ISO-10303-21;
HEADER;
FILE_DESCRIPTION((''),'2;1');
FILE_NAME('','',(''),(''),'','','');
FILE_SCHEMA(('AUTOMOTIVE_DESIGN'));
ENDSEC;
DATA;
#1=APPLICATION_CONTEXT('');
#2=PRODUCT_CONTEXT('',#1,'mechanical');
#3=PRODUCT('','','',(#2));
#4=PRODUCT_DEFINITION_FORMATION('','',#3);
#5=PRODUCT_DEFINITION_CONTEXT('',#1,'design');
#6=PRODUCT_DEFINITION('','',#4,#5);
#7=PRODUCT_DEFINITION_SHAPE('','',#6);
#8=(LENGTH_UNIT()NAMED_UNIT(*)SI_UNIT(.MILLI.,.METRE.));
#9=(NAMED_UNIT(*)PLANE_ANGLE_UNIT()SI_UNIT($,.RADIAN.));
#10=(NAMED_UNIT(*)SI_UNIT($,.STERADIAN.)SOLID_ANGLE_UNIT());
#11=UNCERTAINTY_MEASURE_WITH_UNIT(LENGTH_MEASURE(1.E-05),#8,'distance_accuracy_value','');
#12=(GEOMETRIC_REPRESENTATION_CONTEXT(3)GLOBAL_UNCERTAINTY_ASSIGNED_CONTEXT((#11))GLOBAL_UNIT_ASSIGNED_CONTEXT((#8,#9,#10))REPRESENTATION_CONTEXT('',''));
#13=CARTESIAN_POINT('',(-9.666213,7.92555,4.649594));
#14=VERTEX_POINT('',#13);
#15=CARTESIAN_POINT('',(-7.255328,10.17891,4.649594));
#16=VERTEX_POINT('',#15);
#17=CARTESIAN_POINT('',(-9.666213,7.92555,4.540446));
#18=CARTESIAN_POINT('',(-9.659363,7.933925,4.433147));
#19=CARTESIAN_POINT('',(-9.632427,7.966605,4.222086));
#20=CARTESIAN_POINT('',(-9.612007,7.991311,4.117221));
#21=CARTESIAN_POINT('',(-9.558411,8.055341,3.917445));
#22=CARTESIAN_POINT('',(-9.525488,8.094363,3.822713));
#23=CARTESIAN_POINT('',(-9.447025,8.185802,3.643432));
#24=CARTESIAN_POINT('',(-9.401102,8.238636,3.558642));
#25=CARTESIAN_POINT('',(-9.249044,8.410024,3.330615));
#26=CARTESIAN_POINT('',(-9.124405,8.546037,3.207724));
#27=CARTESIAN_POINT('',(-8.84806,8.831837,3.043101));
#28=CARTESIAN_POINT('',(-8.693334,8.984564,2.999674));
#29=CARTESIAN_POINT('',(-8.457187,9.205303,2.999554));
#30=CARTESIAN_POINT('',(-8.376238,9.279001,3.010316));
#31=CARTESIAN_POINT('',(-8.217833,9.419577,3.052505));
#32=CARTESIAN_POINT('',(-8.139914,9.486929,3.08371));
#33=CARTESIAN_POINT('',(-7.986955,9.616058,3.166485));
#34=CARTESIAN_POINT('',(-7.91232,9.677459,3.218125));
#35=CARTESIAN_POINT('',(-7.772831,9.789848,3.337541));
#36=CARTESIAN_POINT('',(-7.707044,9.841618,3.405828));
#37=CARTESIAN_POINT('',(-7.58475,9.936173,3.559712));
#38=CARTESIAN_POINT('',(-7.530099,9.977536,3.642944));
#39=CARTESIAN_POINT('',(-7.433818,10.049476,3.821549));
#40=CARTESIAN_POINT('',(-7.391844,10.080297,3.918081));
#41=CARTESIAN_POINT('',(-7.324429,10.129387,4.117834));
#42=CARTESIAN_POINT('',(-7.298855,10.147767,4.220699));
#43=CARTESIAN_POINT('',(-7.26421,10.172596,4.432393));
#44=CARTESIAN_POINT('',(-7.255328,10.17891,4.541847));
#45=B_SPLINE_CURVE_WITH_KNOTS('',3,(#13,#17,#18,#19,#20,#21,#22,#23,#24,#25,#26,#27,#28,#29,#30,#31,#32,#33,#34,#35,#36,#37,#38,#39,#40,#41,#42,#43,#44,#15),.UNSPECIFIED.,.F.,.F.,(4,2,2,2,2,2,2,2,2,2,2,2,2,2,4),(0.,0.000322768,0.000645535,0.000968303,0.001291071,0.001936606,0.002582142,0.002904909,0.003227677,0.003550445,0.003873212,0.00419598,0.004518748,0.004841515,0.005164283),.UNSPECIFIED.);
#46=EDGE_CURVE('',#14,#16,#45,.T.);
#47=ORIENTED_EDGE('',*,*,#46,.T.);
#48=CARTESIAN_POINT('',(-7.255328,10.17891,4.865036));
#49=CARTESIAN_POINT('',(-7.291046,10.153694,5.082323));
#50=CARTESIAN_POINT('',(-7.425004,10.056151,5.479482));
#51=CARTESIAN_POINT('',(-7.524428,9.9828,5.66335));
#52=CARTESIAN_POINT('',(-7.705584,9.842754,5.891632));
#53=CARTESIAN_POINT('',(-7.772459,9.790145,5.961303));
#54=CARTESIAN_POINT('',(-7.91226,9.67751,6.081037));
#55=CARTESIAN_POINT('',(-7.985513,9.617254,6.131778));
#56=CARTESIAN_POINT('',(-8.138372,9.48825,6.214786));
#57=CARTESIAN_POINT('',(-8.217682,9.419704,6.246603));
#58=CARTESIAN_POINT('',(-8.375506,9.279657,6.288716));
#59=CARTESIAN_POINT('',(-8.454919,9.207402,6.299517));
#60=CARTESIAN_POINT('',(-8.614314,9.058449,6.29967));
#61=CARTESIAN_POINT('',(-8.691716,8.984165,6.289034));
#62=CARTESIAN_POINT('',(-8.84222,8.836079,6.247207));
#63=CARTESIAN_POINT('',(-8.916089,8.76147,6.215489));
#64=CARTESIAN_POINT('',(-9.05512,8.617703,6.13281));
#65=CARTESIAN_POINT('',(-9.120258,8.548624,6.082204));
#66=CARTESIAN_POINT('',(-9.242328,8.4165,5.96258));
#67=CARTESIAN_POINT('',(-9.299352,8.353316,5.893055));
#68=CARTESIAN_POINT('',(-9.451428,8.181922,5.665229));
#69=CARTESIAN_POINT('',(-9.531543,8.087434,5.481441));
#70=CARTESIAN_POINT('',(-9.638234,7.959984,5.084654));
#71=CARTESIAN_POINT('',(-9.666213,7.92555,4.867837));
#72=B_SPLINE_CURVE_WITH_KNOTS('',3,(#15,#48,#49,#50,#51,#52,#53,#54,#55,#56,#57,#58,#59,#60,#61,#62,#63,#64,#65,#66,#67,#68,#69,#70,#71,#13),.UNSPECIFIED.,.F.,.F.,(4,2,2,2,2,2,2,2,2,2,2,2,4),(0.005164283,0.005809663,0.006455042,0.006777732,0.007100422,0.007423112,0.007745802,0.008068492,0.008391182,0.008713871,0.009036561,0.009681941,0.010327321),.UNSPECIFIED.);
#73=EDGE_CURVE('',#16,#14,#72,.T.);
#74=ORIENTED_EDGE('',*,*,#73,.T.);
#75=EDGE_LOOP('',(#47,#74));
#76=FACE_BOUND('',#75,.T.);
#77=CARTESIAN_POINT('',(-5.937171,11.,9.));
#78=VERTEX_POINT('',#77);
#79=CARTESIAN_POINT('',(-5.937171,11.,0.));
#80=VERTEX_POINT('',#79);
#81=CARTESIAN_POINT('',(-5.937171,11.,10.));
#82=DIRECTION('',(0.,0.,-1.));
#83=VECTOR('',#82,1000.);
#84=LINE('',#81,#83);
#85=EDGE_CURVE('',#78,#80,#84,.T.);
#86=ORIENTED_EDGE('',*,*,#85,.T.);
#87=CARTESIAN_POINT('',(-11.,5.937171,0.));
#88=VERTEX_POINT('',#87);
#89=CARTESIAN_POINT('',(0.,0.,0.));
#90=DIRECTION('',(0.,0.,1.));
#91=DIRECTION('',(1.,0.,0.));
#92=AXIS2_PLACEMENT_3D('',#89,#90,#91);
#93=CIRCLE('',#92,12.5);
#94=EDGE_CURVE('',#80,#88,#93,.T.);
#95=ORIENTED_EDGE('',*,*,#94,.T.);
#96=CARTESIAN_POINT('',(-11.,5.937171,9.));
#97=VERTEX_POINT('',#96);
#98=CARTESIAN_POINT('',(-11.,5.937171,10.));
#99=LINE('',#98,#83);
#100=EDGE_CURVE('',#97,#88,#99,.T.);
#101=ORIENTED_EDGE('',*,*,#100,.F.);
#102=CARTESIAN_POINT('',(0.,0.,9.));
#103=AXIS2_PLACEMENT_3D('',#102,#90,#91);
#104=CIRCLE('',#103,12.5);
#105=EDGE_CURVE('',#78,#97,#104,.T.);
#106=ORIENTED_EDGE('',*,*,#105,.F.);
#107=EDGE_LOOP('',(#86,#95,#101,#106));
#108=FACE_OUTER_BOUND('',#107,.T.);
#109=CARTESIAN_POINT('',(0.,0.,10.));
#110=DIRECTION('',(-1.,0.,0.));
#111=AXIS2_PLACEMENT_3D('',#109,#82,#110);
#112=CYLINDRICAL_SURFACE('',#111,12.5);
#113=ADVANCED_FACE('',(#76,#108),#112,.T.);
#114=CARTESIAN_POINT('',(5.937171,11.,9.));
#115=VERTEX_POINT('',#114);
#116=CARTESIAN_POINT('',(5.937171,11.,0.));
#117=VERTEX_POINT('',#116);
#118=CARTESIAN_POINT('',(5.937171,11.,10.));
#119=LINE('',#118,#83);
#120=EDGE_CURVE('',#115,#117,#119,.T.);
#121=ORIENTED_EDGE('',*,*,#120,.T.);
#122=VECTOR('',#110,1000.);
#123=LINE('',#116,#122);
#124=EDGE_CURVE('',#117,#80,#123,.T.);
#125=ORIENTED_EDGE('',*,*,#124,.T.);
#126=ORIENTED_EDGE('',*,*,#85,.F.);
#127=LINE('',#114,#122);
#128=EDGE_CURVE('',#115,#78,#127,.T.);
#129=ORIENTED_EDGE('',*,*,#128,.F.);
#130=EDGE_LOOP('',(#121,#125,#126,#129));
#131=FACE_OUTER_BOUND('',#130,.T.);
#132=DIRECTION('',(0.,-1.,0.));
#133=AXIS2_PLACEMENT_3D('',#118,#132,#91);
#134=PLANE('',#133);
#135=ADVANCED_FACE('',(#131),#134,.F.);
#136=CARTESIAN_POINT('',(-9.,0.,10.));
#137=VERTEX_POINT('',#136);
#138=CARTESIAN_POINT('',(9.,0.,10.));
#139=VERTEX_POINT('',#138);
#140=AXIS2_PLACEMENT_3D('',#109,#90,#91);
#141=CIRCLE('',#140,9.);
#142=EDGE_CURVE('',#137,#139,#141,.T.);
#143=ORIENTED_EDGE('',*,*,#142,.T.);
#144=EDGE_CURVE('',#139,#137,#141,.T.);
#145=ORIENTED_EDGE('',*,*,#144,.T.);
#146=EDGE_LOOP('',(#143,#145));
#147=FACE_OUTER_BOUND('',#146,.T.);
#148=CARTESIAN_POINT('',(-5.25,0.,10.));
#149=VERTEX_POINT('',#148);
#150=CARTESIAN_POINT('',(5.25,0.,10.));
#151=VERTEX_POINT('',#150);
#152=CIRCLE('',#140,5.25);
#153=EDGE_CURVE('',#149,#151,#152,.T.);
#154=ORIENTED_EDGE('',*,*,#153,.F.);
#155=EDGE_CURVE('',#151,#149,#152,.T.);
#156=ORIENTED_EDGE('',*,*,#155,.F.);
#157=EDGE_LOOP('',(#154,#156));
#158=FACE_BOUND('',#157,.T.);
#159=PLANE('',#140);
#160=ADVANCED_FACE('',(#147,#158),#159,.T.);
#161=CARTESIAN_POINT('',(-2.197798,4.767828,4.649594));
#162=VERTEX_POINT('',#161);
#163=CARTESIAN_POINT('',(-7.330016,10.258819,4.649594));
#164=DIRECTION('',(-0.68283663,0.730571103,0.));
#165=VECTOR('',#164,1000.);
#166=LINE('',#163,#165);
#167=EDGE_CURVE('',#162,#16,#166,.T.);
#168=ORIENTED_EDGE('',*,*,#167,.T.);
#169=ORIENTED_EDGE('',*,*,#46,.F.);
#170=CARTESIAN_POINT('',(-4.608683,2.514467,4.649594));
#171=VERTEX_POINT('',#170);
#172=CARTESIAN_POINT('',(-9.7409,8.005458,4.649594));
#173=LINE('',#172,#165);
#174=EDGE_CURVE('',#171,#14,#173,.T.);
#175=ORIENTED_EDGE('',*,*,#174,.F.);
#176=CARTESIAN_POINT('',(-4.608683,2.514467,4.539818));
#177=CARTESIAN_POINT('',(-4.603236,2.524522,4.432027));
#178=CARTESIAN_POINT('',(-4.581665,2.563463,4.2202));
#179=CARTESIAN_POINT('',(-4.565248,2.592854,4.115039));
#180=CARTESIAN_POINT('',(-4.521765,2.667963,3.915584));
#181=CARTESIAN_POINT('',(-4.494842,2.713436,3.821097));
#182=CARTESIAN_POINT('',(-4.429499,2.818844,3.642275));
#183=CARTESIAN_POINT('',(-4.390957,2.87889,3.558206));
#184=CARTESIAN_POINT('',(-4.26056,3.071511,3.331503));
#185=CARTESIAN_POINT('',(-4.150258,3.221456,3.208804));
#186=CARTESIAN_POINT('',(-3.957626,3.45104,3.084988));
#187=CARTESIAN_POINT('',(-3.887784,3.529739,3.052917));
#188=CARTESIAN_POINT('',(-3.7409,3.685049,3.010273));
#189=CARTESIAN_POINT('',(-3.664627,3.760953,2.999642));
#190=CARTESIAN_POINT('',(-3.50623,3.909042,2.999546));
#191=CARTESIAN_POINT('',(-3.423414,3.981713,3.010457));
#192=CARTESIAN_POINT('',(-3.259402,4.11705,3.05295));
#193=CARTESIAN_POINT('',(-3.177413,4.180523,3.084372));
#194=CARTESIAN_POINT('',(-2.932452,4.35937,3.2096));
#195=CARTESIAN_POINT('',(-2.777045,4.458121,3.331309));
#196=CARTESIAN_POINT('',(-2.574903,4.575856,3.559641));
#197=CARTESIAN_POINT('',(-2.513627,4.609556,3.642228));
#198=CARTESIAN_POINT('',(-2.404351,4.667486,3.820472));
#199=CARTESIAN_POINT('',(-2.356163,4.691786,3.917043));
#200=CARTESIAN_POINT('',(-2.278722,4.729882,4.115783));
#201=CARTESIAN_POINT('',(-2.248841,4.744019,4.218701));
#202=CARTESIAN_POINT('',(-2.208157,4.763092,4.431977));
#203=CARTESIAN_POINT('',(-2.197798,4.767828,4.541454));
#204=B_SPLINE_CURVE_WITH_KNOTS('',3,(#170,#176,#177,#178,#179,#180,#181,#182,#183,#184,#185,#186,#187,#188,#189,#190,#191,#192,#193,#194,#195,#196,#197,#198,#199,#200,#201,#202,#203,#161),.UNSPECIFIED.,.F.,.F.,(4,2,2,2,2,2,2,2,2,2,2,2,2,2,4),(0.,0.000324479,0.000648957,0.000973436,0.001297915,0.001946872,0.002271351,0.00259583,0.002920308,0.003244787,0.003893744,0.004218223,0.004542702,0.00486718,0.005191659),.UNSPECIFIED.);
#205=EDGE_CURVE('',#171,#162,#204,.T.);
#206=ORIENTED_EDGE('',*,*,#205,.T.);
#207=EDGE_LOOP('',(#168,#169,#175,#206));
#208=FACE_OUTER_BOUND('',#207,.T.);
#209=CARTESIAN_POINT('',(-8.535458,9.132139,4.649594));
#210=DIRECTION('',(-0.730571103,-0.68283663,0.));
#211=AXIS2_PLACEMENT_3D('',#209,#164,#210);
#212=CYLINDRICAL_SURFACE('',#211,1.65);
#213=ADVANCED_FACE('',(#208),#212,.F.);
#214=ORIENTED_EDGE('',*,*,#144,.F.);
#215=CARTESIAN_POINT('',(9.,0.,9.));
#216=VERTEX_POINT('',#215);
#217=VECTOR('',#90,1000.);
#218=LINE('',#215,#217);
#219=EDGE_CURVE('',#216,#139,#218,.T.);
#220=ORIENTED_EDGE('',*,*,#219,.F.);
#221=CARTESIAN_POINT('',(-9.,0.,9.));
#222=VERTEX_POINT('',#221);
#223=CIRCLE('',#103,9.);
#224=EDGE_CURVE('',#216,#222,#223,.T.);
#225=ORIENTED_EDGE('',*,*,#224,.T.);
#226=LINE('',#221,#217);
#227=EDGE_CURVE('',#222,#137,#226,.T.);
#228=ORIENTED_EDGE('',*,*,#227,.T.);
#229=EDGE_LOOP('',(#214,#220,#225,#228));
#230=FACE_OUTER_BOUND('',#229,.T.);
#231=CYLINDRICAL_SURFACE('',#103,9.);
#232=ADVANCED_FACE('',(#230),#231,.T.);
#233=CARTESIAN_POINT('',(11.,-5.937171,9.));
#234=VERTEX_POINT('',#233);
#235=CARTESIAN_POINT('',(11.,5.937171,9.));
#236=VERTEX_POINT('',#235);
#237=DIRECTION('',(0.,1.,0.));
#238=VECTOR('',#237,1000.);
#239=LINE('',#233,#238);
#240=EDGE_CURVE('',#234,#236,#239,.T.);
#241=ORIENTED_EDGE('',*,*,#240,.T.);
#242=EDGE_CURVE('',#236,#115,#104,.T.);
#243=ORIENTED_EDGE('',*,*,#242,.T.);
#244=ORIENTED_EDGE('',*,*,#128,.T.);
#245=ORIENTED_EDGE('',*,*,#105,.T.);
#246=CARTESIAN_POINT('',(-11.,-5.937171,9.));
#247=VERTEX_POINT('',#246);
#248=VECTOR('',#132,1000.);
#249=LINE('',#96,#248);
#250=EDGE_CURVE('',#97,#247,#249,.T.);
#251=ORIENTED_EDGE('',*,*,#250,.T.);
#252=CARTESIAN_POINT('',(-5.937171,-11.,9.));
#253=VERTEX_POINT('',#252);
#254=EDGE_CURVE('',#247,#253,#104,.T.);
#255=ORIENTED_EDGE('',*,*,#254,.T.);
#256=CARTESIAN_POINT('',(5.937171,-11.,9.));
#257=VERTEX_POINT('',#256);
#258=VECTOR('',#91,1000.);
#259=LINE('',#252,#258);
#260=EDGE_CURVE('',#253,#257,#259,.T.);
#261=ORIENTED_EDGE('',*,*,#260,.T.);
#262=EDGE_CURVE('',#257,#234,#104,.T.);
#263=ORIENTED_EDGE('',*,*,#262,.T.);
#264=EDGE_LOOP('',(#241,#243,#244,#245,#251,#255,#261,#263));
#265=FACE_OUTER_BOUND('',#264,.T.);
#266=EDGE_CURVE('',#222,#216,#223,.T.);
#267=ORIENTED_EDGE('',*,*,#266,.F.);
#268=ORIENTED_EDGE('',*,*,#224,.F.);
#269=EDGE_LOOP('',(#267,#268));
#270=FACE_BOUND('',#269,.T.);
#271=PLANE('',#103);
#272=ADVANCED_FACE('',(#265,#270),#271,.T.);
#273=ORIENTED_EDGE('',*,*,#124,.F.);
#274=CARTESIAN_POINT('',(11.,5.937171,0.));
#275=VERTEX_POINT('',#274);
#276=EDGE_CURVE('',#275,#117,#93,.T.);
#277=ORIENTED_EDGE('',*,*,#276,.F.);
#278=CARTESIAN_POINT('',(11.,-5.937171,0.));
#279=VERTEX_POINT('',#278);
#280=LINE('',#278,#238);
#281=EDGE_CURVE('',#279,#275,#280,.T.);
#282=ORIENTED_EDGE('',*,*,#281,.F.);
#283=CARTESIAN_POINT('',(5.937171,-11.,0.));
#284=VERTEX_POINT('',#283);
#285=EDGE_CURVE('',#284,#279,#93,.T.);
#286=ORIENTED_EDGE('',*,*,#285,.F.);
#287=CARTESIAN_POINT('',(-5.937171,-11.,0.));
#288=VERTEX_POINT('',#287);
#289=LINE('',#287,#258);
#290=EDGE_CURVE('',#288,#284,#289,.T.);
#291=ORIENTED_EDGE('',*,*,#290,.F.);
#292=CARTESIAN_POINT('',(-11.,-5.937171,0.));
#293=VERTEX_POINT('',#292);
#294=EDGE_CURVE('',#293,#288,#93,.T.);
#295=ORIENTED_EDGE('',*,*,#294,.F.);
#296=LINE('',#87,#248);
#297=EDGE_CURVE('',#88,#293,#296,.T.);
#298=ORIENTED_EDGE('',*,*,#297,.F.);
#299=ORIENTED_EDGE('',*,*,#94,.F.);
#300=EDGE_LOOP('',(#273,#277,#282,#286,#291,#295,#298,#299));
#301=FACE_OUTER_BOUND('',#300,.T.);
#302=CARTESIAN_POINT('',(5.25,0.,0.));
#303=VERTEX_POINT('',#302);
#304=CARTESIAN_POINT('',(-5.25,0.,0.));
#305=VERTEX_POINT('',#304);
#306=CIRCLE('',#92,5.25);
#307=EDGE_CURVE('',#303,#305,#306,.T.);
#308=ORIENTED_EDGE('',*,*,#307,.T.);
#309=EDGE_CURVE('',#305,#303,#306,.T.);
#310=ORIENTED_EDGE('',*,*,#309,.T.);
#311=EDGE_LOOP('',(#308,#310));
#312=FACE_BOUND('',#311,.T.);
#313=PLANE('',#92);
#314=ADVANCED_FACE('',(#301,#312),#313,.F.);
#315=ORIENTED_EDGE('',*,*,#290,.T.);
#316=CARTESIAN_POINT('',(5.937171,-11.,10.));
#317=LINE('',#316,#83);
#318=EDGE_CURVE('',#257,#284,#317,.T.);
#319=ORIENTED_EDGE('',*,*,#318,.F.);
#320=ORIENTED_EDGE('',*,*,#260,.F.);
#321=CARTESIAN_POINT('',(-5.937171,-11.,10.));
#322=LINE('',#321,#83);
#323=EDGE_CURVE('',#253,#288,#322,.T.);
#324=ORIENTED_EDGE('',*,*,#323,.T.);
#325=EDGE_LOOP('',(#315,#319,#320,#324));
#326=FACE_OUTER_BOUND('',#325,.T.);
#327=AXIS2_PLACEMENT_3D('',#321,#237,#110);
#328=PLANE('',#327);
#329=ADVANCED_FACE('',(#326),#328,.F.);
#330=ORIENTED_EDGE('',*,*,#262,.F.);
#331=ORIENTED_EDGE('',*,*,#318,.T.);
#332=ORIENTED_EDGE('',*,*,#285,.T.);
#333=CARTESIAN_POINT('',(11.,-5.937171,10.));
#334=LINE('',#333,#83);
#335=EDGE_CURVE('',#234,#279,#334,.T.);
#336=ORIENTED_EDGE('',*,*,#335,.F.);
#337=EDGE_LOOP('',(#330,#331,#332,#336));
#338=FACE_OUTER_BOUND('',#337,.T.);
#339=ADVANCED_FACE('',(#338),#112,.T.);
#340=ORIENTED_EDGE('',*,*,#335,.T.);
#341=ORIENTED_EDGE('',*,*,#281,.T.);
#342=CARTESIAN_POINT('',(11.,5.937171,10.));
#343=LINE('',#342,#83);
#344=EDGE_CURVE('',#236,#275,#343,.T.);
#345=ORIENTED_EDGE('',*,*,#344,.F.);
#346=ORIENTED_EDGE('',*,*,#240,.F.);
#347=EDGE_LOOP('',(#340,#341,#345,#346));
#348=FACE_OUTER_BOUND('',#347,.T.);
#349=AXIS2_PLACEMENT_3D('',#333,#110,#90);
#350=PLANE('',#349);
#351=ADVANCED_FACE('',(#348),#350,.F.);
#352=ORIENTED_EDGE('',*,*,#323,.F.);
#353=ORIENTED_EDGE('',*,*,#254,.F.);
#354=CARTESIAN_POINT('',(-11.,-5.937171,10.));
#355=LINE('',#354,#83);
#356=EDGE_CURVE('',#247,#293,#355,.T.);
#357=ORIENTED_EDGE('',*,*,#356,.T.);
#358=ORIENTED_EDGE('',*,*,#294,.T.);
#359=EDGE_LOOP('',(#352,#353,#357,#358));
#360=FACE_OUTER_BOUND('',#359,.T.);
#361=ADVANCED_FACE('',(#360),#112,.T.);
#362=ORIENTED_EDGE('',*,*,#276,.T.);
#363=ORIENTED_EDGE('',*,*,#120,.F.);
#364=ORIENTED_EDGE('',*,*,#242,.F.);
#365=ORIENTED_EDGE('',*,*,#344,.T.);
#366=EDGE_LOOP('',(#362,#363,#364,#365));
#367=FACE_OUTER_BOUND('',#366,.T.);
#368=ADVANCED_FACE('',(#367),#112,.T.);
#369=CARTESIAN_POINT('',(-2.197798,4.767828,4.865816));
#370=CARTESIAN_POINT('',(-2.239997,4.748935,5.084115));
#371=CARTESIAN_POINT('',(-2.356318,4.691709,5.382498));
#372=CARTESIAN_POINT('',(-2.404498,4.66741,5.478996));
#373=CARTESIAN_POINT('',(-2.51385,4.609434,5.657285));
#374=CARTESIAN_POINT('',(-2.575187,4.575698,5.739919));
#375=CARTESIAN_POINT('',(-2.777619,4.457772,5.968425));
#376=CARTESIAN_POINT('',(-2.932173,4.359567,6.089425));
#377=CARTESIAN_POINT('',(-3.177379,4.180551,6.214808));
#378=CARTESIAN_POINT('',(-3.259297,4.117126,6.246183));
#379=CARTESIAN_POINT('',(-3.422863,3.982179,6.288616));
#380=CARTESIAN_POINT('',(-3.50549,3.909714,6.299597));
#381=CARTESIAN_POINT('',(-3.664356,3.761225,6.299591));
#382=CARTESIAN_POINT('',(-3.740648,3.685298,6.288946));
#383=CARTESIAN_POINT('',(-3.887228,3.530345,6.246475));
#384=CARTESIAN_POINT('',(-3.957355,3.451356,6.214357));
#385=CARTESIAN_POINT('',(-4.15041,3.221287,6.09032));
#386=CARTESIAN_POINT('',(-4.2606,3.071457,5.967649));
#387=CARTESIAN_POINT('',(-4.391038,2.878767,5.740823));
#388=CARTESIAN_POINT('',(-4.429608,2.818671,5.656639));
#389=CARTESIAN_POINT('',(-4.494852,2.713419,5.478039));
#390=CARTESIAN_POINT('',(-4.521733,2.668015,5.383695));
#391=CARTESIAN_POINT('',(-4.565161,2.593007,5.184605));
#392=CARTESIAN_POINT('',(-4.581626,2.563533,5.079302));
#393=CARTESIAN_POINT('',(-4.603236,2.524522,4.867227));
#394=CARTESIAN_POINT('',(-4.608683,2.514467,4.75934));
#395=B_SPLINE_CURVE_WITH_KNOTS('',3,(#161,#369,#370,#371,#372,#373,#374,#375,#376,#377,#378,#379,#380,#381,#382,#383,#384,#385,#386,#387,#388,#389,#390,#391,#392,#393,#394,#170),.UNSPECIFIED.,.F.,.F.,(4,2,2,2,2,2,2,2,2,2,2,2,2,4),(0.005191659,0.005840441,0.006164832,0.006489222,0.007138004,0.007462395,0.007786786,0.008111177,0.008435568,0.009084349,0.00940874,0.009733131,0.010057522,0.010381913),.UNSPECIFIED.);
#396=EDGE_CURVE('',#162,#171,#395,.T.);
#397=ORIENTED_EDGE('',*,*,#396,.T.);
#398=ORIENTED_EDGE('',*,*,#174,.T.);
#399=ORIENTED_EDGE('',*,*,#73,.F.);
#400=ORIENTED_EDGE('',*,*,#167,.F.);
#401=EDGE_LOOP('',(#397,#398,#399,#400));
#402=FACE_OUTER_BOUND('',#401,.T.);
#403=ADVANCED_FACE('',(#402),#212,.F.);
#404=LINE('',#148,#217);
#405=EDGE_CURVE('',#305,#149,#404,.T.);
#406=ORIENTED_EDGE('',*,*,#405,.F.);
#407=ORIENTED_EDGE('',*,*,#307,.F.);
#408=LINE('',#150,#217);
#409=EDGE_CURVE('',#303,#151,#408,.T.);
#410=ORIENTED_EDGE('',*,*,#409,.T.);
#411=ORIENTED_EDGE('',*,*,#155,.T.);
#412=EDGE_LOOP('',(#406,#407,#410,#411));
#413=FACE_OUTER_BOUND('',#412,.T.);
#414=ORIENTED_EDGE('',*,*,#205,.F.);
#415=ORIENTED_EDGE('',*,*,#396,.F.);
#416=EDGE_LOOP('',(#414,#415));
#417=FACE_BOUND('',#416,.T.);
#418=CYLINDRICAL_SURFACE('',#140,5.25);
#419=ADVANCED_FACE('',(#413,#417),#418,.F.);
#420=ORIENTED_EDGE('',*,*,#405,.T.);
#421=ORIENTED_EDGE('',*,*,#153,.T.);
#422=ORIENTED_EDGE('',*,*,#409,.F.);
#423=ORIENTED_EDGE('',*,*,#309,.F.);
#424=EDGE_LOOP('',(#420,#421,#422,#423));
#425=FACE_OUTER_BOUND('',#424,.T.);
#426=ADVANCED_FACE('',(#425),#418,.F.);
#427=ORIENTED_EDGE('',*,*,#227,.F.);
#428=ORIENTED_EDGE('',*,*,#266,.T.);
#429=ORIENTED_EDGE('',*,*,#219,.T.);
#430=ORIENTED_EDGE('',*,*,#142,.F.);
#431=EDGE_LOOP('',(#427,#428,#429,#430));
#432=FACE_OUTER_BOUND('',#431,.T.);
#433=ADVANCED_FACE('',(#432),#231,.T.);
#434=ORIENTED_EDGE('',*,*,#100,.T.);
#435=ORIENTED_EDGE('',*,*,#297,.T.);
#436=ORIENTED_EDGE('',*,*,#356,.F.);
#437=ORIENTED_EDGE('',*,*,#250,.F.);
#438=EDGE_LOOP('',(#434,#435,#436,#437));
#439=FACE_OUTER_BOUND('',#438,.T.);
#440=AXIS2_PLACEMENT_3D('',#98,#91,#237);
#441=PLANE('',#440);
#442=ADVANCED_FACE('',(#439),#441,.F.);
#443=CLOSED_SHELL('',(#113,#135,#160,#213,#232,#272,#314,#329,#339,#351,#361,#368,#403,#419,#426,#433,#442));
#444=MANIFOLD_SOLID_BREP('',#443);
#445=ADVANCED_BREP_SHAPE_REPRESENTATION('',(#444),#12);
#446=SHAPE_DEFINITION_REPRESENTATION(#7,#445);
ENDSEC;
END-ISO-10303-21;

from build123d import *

# Parameters (mm, degrees)
EXTRUDE1_DEPTH             = 10
SKETCH2_OUTSIDE_W          = 30.536
SKETCH2_OUTSIDE_H          = 30.536
SKETCH2_OUTSIDE_R          = 9
EXTRUDE2_DEPTH             = 1
M4X0_7_TAPPED_HOLE1_D      = 3.3
M4X0_7_TAPPED_HOLE1_DEPTH  = 10.1
M4X0_7_TAPPED_HOLE1_TIP    = 0.991420021
M12X1_5_TAPPED_HOLE1_D     = 10.5
M12X1_5_TAPPED_HOLE1_DEPTH = 28.5
M12X1_5_TAPPED_HOLE1_TIP   = 3.15451825


with BuildPart() as part:
    # Sketch1 → Extrude1 (new body)
    with BuildSketch(Plane.XY):
        with BuildLine():
            Line((-5.937171043, -11), (5.937171043, -11))
            ThreePointArc((5.937171043, -11), (8.838834765, -8.838834765), (11, -5.937171043))
            Line((11, -5.937171043), (11, 5.937171043))
            ThreePointArc((11, 5.937171043), (8.838834765, 8.838834765), (5.937171043, 11))
            Line((5.937171043, 11), (-5.937171043, 11))
            ThreePointArc((-5.937171043, 11), (-8.838834765, 8.838834765), (-11, 5.937171043))
            Line((-11, 5.937171043), (-11, -5.937171043))
            ThreePointArc((-11, -5.937171043), (-8.838834765, -8.838834765), (-5.937171043, -11))
        make_face()
    extrude(amount=EXTRUDE1_DEPTH)

    # Sketch2 outside → Extrude2 (cut)
    with BuildSketch(Plane.XY.offset(10)):
        Rectangle(SKETCH2_OUTSIDE_W, SKETCH2_OUTSIDE_H)
        Circle(SKETCH2_OUTSIDE_R, mode=Mode.SUBTRACT)
    extrude(amount=-EXTRUDE2_DEPTH, mode=Mode.SUBTRACT)

    # M4x0.7 Tapped Hole1
    with Locations(Plane(origin=(-8.535457879, 9.132138785, 4.649594026), x_dir=(0.730571102805, 0.682836630349, 0), z_dir=(-0.682836630349, 0.730571102805, 0))):
        with Locations((0, 0)):
            Hole(M4X0_7_TAPPED_HOLE1_D / 2, depth=M4X0_7_TAPPED_HOLE1_DEPTH)
            with Locations((0, 0, -(M4X0_7_TAPPED_HOLE1_DEPTH + M4X0_7_TAPPED_HOLE1_TIP / 2))):  # 118° drill point
                Cone(0, M4X0_7_TAPPED_HOLE1_D / 2, M4X0_7_TAPPED_HOLE1_TIP, mode=Mode.SUBTRACT)

    # M12x1.5 Tapped Hole1
    with Locations(Plane.XY.offset(10)):
        with Locations((0, 0)):
            Hole(M12X1_5_TAPPED_HOLE1_D / 2, depth=M12X1_5_TAPPED_HOLE1_DEPTH)
            with Locations((0, 0, -(M12X1_5_TAPPED_HOLE1_DEPTH + M12X1_5_TAPPED_HOLE1_TIP / 2))):  # 118° drill point
                Cone(0, M12X1_5_TAPPED_HOLE1_D / 2, M12X1_5_TAPPED_HOLE1_TIP, mode=Mode.SUBTRACT)


solid = part.part
